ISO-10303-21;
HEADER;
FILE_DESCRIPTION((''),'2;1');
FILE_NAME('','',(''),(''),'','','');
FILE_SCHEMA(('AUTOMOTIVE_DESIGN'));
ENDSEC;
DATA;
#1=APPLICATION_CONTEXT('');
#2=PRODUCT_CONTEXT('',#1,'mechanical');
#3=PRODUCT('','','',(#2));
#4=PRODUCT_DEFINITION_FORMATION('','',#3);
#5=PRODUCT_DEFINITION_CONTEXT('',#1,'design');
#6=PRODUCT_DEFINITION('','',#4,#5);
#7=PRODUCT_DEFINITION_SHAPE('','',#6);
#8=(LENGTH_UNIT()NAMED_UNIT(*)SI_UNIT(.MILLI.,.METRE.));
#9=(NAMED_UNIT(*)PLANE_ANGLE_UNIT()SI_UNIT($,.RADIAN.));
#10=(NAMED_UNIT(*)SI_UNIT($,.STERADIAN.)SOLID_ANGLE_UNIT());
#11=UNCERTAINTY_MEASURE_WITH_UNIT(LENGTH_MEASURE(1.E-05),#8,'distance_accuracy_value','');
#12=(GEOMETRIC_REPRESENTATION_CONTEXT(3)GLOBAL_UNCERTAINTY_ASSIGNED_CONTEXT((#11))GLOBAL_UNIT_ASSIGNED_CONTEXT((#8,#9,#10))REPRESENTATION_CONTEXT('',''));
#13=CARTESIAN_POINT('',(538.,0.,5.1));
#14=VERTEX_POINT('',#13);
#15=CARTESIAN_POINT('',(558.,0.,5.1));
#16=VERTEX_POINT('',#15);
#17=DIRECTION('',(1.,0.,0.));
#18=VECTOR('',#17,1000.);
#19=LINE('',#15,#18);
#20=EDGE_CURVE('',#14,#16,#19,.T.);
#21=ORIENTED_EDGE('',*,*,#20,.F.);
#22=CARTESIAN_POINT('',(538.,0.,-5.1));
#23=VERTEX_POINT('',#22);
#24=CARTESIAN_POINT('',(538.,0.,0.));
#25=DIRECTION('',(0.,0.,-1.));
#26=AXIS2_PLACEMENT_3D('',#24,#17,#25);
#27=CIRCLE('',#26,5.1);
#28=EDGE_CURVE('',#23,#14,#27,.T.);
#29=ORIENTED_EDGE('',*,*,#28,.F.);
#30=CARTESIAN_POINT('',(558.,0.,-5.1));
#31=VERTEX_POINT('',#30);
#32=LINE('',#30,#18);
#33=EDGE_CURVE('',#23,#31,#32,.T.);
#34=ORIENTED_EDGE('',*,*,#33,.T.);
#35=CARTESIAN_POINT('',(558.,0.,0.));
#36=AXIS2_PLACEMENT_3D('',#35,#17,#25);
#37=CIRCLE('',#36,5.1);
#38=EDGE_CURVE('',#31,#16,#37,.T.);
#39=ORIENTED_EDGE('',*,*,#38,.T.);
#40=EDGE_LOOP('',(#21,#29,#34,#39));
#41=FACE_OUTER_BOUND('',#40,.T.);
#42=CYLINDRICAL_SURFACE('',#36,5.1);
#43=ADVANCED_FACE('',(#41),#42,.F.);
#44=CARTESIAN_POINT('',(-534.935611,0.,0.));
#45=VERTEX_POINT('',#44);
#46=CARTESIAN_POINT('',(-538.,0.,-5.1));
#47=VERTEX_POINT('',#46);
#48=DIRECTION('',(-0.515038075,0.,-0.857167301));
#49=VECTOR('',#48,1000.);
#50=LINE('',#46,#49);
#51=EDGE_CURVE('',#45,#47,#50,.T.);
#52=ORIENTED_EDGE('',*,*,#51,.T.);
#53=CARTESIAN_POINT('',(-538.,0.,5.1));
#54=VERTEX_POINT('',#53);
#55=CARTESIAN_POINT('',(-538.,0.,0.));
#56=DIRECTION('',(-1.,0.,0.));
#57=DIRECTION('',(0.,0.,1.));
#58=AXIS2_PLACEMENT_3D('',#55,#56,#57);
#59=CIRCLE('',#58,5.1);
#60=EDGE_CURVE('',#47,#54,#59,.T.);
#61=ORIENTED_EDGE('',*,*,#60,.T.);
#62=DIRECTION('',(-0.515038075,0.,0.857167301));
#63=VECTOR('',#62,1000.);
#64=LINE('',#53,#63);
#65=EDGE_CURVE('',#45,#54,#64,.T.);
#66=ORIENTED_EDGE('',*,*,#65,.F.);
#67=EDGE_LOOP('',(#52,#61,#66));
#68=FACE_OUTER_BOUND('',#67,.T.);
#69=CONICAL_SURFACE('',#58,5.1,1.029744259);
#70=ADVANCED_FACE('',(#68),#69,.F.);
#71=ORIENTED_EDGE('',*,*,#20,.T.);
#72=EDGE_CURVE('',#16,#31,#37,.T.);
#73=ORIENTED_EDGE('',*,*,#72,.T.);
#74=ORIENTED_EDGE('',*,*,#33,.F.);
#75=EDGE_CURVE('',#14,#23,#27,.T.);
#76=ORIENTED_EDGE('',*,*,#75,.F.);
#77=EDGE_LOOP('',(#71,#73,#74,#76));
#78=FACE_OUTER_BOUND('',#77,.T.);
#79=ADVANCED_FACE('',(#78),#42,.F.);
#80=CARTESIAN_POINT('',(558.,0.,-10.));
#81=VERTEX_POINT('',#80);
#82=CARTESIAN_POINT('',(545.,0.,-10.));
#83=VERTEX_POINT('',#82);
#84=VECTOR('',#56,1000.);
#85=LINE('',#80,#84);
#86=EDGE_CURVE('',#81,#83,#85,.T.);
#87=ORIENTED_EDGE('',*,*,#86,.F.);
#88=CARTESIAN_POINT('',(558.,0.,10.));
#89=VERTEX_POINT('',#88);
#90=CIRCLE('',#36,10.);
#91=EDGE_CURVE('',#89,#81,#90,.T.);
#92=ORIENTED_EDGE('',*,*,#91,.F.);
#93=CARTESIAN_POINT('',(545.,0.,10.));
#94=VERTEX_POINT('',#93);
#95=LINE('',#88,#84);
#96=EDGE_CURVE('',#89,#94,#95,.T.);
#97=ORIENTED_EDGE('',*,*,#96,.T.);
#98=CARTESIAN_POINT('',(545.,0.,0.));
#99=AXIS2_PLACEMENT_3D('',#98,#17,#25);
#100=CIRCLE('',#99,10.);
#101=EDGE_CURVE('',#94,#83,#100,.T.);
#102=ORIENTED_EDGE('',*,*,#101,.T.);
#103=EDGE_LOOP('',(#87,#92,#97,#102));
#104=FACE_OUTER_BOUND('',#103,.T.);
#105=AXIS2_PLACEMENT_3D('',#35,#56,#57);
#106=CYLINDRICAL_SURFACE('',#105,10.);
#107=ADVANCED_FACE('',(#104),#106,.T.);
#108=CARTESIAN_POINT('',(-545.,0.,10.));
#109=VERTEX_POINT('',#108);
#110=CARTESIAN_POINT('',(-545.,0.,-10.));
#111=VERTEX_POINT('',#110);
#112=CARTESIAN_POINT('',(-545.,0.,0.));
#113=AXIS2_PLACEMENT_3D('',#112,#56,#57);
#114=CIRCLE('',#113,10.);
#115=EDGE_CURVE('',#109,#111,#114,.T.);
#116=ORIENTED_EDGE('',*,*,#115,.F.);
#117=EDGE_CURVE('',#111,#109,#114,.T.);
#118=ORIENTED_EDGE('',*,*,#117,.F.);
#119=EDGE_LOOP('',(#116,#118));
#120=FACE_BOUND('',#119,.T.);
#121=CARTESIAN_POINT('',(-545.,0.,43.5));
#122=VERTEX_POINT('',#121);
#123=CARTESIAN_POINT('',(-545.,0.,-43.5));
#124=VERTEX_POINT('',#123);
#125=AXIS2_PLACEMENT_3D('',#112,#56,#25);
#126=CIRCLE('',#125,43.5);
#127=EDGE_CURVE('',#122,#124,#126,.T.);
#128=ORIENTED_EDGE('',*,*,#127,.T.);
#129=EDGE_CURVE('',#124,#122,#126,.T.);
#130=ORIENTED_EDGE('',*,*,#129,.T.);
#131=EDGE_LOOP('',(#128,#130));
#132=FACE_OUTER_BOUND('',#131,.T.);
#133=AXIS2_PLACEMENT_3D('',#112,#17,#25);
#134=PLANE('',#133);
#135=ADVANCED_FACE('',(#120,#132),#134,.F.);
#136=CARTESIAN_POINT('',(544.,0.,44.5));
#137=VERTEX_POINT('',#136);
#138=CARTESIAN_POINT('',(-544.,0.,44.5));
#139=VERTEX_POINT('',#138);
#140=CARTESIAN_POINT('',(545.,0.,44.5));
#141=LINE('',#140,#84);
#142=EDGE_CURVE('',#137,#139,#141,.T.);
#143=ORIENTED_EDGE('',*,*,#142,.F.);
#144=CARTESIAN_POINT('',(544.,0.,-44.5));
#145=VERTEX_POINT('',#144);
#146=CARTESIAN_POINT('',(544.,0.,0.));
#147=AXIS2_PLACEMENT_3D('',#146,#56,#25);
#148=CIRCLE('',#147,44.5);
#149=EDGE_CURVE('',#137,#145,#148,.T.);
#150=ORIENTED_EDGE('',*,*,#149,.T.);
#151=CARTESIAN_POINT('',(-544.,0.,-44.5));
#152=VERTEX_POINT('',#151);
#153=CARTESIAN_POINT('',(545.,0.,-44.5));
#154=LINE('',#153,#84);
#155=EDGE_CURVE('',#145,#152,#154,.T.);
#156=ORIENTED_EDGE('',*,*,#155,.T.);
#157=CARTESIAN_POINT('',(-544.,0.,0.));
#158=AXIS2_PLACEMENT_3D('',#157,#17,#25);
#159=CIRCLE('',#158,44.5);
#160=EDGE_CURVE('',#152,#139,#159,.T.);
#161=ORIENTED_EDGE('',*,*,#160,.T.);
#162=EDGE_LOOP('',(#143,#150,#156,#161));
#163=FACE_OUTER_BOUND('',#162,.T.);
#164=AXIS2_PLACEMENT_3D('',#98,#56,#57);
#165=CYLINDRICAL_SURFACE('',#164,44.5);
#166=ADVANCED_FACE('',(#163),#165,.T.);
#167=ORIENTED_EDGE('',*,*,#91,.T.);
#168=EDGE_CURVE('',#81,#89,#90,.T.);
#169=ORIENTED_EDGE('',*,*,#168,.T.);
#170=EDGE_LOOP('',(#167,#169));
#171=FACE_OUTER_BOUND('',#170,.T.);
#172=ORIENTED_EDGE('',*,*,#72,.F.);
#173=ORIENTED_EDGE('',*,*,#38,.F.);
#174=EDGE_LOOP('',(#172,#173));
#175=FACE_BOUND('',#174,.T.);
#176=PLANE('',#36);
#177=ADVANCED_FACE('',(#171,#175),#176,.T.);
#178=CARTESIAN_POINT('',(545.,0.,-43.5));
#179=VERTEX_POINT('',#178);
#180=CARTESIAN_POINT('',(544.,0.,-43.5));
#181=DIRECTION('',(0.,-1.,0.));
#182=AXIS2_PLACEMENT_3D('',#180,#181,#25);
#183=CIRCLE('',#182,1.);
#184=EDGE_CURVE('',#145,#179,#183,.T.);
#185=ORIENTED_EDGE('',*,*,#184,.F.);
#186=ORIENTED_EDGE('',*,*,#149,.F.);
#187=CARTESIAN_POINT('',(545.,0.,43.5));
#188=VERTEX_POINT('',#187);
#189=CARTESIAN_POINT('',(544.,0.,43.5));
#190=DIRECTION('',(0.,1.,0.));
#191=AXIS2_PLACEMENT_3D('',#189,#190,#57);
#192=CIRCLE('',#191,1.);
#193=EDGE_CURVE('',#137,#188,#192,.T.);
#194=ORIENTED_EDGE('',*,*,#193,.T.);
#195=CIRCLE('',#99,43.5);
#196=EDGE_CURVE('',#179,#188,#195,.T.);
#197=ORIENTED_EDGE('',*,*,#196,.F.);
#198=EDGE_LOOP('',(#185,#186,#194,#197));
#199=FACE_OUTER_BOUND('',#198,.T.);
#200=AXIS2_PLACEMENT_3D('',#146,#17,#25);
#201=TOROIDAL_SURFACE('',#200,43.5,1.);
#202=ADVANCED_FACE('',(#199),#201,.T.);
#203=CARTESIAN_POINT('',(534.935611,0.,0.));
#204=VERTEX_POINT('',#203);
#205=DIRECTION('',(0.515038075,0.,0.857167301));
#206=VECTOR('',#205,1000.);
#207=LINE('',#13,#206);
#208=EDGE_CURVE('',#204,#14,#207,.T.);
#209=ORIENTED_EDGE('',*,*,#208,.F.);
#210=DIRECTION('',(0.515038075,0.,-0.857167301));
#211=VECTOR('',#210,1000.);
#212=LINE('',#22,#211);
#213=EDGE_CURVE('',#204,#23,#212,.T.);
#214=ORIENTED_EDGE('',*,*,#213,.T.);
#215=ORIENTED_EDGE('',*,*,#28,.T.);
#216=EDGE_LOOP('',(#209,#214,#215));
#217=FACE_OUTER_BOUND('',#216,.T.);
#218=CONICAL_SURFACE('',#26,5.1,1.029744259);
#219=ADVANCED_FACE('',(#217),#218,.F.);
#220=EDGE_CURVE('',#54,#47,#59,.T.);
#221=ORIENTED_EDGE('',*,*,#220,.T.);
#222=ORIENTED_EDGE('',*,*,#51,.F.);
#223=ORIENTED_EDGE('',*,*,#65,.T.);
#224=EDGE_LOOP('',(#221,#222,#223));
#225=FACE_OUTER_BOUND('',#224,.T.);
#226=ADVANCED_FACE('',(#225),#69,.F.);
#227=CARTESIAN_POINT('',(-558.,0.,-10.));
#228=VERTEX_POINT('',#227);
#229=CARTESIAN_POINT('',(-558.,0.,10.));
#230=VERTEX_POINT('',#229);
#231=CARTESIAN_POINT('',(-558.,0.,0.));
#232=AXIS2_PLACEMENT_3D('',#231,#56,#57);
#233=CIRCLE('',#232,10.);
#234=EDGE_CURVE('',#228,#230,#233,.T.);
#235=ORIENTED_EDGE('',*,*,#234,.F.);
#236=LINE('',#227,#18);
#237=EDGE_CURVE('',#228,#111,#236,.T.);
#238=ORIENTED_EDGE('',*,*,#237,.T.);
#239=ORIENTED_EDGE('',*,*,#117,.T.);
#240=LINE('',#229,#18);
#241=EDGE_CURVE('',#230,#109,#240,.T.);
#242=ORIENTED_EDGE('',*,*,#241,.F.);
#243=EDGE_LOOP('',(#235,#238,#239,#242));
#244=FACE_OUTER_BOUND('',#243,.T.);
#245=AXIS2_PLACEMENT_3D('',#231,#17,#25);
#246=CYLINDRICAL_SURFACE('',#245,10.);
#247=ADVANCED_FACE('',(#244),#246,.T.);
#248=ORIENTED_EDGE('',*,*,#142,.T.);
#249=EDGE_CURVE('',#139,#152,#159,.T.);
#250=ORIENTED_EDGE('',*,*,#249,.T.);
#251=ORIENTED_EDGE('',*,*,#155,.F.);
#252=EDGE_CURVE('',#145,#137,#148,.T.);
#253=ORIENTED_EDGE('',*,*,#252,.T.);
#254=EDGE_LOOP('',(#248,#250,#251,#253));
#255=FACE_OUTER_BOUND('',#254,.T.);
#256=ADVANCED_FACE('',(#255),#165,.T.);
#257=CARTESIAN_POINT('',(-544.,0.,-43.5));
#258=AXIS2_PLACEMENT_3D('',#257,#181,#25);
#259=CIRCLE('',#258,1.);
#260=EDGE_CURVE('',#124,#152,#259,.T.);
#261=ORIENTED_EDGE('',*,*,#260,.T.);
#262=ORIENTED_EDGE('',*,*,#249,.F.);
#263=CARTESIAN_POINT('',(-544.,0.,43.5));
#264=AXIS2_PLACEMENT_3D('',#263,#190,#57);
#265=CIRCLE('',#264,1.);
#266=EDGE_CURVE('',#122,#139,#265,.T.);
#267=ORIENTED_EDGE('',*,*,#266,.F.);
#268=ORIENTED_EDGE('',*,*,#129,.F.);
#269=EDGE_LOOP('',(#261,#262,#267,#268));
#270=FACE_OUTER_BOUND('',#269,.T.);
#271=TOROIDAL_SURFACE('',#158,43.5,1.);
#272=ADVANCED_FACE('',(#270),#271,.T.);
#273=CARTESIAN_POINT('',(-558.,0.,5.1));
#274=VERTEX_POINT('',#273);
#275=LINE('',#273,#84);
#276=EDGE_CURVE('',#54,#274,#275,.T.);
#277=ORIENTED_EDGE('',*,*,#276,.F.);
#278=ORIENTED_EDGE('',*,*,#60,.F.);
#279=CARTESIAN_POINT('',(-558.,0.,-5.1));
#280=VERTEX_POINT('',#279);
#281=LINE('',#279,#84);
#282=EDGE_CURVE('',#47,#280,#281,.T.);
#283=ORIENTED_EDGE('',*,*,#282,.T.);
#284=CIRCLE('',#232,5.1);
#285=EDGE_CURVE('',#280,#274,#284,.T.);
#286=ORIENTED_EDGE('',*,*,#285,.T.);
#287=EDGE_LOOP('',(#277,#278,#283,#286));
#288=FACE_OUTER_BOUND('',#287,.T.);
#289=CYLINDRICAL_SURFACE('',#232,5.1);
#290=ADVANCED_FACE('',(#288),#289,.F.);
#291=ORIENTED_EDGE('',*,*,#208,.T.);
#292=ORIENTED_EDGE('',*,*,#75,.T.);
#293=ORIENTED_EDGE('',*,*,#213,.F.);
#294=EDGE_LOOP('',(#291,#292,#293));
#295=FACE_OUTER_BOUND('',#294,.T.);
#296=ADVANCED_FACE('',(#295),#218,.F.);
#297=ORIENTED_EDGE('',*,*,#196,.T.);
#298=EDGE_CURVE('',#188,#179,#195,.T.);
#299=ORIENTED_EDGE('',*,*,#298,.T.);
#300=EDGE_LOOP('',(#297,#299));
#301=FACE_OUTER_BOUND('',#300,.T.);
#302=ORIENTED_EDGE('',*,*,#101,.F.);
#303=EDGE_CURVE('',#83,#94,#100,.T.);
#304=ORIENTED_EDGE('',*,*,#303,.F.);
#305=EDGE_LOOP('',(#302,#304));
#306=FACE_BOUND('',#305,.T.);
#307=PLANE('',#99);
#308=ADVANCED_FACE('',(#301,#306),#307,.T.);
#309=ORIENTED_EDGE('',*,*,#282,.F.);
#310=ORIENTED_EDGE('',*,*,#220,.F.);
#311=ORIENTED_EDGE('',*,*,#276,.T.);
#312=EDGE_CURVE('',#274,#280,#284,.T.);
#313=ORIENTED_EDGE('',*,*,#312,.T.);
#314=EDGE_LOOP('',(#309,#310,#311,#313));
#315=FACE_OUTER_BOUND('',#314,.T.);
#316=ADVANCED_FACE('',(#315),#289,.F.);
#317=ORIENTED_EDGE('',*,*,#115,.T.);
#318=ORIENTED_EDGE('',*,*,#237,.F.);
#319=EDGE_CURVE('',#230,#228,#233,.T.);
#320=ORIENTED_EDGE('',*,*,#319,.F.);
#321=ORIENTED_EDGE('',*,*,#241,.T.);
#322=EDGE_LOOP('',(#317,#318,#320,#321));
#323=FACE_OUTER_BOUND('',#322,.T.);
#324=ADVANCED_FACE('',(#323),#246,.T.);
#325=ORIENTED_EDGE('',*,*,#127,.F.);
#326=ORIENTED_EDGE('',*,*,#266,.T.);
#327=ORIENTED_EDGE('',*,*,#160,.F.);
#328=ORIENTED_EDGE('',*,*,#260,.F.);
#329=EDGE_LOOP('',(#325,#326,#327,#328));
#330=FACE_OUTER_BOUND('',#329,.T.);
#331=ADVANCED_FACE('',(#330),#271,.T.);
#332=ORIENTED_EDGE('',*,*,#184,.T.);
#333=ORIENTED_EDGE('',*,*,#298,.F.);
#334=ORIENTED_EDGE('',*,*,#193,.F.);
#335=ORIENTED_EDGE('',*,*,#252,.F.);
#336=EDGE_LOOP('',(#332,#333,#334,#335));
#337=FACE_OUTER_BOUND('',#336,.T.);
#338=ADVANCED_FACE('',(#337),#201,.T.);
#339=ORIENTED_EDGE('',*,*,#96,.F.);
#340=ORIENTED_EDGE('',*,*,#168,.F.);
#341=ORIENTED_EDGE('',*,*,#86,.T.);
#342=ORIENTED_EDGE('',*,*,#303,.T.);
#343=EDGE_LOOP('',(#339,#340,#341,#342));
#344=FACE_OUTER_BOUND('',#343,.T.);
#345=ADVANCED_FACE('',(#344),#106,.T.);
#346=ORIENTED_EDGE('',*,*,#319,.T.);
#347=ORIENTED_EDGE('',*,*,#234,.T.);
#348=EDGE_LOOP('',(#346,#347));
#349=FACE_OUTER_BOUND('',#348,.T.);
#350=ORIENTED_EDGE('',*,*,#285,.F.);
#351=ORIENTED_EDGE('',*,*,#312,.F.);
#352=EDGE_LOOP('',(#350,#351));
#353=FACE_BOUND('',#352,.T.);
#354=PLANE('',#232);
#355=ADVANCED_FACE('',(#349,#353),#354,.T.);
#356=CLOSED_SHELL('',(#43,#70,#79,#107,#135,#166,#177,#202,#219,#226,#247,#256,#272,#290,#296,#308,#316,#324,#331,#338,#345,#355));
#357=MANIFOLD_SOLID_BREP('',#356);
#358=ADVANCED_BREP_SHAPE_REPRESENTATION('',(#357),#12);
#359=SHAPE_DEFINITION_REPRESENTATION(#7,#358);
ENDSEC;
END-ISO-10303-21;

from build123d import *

# Parameters (mm, degrees)
SKETCH1_R                        = 44.5
BOSS_EXTRUDE1_DEPTH              = 545
SKETCH2_R                        = 10
BOSS_EXTRUDE2_DEPTH              = 13
BOSS_EXTRUDE3_START              = 13
SKETCH3_R                        = 10
BOSS_EXTRUDE3_DEPTH              = 13
FILLET1_R                        = 1
M12_TAPPED_HOLE1_D               = 10.2
M12_TAPPED_HOLE1_DEPTH           = 20
M12_TAPPED_HOLE1_TIP             = 3.064389157
M12_TAPPED_HOLE1_ON_FACE_2_D     = 10.2
M12_TAPPED_HOLE1_ON_FACE_2_DEPTH = 20
M12_TAPPED_HOLE1_ON_FACE_2_TIP   = 3.064389157


with BuildPart() as part:
    # Sketch1 → Boss-Extrude1 (new, symmetric)
    with BuildSketch(Plane(origin=(0, 0, 0), x_dir=(0, 0, -1), z_dir=(1, 0, 0))):
        Circle(SKETCH1_R)
    extrude(amount=BOSS_EXTRUDE1_DEPTH, both=True)

    # Sketch2 → Boss-Extrude2 (add)
    with BuildSketch(Plane(origin=(545, 0, 0), x_dir=(0, 0, -1), z_dir=(1, 0, 0))):
        with Locations(Location((0, 0, 0), (0, 0, 180))):
            Circle(SKETCH2_R)
    extrude(amount=BOSS_EXTRUDE2_DEPTH)

    # Sketch3 → Boss-Extrude3 (add)
    with BuildSketch(Plane.ZY.offset(545).offset(BOSS_EXTRUDE3_START)):
        Circle(SKETCH3_R)
    extrude(amount=-BOSS_EXTRUDE3_DEPTH)

    # Fillet1
    fillet1_edges = [part.edges().sort_by_distance(p)[0] for p in [
        (-545, 0, 44.5),
        (545, 0, 44.5),
    ]]
    fillet(fillet1_edges, radius=FILLET1_R)

    # M12 Tapped Hole1
    with Locations(Plane(origin=(558, 0, 0), x_dir=(0, 0, 1), z_dir=(1, 0, 0))):
        with Locations((0, 0)):
            Hole(M12_TAPPED_HOLE1_D / 2, depth=M12_TAPPED_HOLE1_DEPTH)
            with Locations((0, 0, -(M12_TAPPED_HOLE1_DEPTH + M12_TAPPED_HOLE1_TIP / 2))):  # 118° drill point
                Cone(0, M12_TAPPED_HOLE1_D / 2, M12_TAPPED_HOLE1_TIP, mode=Mode.SUBTRACT)

    # M12 Tapped Hole1 on face 2
    with Locations(Plane(origin=(-558, 0, 0), x_dir=(0, 0, -1), z_dir=(-1, 0, 0))):
        with Locations((0, 0)):
            Hole(M12_TAPPED_HOLE1_ON_FACE_2_D / 2, depth=M12_TAPPED_HOLE1_ON_FACE_2_DEPTH)
            with Locations((0, 0, -(M12_TAPPED_HOLE1_ON_FACE_2_DEPTH + M12_TAPPED_HOLE1_ON_FACE_2_TIP / 2))):  # 118° drill point
                Cone(0, M12_TAPPED_HOLE1_ON_FACE_2_D / 2, M12_TAPPED_HOLE1_ON_FACE_2_TIP, mode=Mode.SUBTRACT)


solid = part.part
